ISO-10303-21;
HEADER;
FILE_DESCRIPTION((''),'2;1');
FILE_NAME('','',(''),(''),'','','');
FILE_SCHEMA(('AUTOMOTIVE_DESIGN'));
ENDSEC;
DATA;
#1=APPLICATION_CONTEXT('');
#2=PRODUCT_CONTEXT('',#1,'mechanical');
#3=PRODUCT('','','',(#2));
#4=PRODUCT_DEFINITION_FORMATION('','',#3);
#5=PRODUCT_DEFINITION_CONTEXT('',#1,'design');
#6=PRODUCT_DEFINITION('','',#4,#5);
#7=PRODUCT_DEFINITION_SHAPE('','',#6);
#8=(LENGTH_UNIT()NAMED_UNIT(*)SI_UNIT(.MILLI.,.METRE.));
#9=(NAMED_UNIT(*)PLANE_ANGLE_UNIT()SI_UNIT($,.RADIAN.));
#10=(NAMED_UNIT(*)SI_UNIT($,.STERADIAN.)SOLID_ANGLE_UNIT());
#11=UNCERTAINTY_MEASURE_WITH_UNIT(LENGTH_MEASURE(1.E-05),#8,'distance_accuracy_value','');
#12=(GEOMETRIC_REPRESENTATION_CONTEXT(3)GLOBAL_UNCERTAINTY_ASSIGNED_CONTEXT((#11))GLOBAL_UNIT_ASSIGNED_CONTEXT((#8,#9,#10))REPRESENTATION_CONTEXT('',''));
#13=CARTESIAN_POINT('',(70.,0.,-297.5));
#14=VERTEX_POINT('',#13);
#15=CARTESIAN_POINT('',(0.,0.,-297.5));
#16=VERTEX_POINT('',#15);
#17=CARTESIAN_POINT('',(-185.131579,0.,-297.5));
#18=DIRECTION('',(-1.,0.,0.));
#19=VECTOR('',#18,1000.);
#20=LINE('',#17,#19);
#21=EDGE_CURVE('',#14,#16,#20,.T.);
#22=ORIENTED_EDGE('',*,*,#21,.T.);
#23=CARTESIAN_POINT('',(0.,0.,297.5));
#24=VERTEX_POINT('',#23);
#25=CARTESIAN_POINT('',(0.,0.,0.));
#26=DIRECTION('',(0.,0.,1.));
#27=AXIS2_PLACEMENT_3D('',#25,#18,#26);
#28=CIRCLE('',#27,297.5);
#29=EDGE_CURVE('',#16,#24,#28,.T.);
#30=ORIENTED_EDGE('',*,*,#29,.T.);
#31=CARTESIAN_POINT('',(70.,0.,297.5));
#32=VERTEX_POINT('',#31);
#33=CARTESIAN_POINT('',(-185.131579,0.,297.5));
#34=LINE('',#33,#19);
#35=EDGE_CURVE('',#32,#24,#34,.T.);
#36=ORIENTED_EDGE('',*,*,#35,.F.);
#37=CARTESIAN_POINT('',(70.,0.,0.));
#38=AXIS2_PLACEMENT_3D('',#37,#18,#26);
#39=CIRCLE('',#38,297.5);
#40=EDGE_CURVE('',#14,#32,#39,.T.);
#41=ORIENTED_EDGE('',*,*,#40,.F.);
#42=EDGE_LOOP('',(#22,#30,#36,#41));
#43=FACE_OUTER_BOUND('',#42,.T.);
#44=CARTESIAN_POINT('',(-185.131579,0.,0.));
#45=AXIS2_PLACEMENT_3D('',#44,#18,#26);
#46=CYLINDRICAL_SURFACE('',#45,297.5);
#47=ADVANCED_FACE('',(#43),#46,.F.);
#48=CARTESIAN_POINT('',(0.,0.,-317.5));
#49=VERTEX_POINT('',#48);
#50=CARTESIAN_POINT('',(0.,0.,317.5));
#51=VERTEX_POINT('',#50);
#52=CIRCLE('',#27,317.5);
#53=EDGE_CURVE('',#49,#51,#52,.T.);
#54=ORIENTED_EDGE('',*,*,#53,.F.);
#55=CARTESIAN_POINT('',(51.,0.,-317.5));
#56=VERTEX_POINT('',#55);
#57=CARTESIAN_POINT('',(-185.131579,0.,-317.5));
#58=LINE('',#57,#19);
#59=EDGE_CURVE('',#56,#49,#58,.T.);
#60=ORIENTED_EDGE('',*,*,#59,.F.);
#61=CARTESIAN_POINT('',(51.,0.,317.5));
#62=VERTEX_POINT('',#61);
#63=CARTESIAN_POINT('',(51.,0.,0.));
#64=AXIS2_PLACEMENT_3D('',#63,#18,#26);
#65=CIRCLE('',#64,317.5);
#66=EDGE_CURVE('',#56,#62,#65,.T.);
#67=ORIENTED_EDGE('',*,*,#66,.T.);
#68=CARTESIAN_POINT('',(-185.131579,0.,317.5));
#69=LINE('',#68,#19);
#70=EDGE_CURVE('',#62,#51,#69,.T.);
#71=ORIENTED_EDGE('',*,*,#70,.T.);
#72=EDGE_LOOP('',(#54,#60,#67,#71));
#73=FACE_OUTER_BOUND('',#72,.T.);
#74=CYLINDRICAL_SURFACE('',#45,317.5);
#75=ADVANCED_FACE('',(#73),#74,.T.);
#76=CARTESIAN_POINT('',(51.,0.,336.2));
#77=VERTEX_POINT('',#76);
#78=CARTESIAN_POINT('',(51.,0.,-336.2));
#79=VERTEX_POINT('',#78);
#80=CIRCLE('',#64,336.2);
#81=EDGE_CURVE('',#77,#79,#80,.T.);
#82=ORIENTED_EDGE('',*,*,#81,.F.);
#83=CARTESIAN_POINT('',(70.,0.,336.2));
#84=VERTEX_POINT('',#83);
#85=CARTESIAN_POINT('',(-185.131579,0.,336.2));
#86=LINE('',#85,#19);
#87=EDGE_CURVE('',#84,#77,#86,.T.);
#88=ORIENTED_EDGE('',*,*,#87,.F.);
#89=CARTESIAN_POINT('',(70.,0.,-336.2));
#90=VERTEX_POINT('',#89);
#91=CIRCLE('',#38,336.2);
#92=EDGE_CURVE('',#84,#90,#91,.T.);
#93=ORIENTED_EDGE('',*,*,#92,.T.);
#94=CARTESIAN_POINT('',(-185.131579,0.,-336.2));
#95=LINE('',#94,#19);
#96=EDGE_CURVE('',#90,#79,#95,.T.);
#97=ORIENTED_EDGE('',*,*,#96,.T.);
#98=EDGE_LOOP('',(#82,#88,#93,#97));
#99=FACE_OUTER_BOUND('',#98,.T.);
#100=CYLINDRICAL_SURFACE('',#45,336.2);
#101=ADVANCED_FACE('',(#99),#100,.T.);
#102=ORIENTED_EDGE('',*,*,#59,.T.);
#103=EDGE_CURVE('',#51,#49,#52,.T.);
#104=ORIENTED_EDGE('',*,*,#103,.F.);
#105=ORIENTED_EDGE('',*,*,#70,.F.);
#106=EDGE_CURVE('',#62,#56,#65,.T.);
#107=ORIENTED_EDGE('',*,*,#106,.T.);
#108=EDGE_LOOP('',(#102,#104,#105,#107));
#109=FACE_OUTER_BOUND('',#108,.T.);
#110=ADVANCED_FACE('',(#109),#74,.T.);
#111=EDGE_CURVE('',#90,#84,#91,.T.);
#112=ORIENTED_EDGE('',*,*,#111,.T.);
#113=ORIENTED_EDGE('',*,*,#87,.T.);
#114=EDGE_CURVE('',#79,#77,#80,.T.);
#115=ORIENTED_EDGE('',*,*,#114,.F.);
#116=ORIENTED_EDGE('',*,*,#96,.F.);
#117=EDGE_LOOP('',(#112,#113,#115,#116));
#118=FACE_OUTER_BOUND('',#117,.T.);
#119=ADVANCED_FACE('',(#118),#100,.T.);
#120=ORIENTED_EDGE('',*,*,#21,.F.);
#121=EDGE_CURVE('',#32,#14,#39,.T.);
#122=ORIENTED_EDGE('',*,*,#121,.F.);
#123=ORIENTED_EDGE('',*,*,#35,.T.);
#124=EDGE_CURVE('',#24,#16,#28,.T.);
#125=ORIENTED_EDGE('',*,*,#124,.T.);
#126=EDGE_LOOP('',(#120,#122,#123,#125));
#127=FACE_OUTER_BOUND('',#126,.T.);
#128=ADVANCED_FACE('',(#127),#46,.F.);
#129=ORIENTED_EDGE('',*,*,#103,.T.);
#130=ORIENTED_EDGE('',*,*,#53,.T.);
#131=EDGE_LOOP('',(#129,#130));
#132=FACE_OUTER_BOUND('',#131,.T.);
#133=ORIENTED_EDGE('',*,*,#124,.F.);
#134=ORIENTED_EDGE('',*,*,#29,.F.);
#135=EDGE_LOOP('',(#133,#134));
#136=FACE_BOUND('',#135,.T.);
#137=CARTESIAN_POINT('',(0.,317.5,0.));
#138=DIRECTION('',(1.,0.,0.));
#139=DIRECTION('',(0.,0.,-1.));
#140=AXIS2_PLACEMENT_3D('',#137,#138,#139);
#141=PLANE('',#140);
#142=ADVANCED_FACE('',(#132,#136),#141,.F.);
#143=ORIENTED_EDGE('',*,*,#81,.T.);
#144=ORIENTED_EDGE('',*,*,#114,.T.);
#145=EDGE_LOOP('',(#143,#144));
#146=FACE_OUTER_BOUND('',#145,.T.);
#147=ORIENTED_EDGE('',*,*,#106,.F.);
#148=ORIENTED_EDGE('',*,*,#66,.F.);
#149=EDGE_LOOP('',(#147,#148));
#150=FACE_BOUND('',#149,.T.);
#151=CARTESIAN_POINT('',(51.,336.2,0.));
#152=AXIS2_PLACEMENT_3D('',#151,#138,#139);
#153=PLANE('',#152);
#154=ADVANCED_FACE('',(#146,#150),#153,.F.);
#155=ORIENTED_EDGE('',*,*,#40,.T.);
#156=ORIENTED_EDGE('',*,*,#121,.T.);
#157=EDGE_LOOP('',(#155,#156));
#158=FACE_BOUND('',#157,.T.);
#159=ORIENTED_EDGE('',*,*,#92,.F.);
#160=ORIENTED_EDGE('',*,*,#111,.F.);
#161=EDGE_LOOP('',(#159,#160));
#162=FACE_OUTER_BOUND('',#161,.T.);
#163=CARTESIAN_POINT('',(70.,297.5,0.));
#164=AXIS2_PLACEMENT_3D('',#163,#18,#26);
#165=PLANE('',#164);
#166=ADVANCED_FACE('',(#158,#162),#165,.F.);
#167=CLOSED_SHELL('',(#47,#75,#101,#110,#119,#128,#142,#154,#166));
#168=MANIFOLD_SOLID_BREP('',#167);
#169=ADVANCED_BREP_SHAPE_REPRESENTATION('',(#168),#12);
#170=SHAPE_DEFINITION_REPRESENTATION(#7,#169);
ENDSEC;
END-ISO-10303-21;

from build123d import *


with BuildPart() as part:
    # 草图1 → 旋转1 (revolve)
    with BuildSketch(Plane.XY, mode=Mode.PRIVATE) as revolve_1_sk:
        Polygon((0, 297.5), (70, 297.5), (70, 336.2), (51, 336.2), (51, 317.5), (0, 317.5), align=None)
    revolve(revolve_1_sk.sketch.rotate(Axis((-185.131578947, 0, 0), (1, 0, 0)), 90), axis=Axis((-185.131578947, 0, 0), (1, 0, 0)))


solid = part.part
